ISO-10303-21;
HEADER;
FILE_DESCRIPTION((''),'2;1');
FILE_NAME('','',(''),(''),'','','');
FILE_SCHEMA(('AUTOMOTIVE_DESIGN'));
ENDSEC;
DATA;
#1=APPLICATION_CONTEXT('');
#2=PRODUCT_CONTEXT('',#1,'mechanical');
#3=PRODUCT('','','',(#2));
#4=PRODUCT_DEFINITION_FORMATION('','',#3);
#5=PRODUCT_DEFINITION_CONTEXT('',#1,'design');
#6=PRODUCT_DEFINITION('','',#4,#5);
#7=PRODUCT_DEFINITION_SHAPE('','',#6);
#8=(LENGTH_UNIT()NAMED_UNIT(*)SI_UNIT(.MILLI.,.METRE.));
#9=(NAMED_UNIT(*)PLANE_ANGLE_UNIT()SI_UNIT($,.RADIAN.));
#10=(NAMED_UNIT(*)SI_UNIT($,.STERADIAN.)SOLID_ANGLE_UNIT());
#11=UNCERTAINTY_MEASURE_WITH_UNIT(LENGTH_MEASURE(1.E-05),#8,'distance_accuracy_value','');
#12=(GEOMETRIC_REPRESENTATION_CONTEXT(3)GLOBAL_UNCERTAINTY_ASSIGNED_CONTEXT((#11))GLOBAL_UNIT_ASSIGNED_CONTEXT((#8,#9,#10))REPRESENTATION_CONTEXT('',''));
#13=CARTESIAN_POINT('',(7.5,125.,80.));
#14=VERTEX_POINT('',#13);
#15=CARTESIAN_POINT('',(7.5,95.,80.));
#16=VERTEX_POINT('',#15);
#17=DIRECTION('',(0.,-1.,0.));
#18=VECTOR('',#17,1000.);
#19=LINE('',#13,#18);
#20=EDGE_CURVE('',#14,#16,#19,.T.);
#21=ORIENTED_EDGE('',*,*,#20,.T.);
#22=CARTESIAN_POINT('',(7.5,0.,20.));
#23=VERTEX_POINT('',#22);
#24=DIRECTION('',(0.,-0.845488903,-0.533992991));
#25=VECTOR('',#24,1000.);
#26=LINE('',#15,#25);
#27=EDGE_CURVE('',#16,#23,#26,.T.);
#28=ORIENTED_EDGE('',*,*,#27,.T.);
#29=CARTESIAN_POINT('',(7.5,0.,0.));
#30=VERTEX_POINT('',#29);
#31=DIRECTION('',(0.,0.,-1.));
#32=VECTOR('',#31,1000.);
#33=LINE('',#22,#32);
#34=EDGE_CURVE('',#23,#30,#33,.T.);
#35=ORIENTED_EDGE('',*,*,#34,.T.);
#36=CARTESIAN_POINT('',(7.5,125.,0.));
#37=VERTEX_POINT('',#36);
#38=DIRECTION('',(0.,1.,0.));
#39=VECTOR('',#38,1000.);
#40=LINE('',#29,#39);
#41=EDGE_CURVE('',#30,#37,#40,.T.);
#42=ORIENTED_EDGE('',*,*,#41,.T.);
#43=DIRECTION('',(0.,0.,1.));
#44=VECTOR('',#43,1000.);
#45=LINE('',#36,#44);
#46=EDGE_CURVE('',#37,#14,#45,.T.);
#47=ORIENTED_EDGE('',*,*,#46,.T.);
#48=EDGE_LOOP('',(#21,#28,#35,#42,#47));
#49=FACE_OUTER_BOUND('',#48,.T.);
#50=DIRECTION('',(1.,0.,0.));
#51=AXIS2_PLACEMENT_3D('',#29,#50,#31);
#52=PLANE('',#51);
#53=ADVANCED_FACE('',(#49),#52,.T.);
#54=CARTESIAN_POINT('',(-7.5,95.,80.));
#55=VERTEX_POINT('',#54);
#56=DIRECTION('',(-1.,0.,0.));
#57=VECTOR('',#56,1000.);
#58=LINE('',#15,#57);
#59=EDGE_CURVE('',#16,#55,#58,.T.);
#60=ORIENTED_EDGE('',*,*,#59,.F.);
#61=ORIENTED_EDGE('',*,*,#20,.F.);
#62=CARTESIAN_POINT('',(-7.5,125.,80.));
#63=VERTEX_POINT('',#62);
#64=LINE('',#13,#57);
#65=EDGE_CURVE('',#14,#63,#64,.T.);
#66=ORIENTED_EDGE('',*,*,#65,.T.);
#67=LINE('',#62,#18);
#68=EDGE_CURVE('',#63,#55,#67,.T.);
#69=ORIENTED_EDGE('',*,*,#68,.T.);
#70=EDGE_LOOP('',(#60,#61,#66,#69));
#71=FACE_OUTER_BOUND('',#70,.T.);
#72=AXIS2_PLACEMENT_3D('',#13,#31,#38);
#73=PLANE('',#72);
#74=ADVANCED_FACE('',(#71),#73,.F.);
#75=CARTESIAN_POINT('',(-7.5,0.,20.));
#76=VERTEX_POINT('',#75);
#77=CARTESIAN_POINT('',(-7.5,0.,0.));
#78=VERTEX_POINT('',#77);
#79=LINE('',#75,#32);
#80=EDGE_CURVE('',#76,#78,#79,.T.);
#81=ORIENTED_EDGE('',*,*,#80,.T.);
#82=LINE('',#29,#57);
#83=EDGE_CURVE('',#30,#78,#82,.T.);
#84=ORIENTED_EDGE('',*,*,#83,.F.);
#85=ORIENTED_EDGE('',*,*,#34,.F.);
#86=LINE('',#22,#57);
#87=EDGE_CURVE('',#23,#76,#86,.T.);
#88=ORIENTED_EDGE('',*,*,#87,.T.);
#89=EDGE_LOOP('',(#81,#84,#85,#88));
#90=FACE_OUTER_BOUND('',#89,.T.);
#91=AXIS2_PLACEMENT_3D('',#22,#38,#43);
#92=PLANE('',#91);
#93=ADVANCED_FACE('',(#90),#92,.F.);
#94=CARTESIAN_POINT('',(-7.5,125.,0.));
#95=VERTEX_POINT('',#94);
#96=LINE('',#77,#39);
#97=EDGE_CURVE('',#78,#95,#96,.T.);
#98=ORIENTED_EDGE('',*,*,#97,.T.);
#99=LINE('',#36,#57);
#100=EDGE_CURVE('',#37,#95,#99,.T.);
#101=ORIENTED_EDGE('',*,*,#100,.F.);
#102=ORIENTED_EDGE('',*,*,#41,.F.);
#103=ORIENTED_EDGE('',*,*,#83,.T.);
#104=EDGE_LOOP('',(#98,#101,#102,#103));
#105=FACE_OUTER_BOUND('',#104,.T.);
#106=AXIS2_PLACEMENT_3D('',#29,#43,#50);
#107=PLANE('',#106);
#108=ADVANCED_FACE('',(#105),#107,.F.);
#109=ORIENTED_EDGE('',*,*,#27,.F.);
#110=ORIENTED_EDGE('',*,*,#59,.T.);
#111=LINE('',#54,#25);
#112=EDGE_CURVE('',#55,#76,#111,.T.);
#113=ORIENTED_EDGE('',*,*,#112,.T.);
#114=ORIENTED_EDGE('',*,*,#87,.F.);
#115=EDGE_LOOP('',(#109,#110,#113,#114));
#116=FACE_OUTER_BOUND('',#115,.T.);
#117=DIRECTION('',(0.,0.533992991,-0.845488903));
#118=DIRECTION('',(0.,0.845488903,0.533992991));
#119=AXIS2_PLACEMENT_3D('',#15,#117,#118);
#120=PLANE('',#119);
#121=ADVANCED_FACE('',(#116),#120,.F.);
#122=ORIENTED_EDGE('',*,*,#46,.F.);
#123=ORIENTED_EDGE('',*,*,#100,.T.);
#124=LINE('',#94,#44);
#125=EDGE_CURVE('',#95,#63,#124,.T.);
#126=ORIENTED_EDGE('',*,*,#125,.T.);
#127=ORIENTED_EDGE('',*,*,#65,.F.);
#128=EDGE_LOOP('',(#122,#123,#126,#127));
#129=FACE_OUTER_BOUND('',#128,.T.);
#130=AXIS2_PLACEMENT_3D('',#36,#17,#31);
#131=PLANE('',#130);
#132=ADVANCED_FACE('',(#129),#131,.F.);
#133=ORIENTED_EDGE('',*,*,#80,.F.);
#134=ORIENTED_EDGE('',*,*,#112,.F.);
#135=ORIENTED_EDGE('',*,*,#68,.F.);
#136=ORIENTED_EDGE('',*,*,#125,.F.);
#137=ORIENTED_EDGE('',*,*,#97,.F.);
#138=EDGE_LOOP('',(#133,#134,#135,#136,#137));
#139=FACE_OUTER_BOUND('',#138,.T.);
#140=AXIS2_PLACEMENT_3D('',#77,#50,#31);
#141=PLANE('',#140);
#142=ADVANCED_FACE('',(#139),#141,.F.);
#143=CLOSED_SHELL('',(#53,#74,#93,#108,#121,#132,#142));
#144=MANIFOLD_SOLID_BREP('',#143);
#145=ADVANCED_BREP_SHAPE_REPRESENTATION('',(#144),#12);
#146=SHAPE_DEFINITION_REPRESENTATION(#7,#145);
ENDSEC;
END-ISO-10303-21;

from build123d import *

# Parameters (mm, degrees)
BOSS_EXTRUDE1_DEPTH = 7.5


with BuildPart() as part:
    # Sketch1 → Boss-Extrude1 (new, symmetric)
    with BuildSketch(Plane(origin=(0, 0, 0), x_dir=(0, 0, -1), z_dir=(1, 0, 0))):
        Polygon((0, 0), (0, 125), (-80, 125), (-80, 95), (-20, 0), align=None)
    extrude(amount=BOSS_EXTRUDE1_DEPTH, both=True)


solid = part.part
